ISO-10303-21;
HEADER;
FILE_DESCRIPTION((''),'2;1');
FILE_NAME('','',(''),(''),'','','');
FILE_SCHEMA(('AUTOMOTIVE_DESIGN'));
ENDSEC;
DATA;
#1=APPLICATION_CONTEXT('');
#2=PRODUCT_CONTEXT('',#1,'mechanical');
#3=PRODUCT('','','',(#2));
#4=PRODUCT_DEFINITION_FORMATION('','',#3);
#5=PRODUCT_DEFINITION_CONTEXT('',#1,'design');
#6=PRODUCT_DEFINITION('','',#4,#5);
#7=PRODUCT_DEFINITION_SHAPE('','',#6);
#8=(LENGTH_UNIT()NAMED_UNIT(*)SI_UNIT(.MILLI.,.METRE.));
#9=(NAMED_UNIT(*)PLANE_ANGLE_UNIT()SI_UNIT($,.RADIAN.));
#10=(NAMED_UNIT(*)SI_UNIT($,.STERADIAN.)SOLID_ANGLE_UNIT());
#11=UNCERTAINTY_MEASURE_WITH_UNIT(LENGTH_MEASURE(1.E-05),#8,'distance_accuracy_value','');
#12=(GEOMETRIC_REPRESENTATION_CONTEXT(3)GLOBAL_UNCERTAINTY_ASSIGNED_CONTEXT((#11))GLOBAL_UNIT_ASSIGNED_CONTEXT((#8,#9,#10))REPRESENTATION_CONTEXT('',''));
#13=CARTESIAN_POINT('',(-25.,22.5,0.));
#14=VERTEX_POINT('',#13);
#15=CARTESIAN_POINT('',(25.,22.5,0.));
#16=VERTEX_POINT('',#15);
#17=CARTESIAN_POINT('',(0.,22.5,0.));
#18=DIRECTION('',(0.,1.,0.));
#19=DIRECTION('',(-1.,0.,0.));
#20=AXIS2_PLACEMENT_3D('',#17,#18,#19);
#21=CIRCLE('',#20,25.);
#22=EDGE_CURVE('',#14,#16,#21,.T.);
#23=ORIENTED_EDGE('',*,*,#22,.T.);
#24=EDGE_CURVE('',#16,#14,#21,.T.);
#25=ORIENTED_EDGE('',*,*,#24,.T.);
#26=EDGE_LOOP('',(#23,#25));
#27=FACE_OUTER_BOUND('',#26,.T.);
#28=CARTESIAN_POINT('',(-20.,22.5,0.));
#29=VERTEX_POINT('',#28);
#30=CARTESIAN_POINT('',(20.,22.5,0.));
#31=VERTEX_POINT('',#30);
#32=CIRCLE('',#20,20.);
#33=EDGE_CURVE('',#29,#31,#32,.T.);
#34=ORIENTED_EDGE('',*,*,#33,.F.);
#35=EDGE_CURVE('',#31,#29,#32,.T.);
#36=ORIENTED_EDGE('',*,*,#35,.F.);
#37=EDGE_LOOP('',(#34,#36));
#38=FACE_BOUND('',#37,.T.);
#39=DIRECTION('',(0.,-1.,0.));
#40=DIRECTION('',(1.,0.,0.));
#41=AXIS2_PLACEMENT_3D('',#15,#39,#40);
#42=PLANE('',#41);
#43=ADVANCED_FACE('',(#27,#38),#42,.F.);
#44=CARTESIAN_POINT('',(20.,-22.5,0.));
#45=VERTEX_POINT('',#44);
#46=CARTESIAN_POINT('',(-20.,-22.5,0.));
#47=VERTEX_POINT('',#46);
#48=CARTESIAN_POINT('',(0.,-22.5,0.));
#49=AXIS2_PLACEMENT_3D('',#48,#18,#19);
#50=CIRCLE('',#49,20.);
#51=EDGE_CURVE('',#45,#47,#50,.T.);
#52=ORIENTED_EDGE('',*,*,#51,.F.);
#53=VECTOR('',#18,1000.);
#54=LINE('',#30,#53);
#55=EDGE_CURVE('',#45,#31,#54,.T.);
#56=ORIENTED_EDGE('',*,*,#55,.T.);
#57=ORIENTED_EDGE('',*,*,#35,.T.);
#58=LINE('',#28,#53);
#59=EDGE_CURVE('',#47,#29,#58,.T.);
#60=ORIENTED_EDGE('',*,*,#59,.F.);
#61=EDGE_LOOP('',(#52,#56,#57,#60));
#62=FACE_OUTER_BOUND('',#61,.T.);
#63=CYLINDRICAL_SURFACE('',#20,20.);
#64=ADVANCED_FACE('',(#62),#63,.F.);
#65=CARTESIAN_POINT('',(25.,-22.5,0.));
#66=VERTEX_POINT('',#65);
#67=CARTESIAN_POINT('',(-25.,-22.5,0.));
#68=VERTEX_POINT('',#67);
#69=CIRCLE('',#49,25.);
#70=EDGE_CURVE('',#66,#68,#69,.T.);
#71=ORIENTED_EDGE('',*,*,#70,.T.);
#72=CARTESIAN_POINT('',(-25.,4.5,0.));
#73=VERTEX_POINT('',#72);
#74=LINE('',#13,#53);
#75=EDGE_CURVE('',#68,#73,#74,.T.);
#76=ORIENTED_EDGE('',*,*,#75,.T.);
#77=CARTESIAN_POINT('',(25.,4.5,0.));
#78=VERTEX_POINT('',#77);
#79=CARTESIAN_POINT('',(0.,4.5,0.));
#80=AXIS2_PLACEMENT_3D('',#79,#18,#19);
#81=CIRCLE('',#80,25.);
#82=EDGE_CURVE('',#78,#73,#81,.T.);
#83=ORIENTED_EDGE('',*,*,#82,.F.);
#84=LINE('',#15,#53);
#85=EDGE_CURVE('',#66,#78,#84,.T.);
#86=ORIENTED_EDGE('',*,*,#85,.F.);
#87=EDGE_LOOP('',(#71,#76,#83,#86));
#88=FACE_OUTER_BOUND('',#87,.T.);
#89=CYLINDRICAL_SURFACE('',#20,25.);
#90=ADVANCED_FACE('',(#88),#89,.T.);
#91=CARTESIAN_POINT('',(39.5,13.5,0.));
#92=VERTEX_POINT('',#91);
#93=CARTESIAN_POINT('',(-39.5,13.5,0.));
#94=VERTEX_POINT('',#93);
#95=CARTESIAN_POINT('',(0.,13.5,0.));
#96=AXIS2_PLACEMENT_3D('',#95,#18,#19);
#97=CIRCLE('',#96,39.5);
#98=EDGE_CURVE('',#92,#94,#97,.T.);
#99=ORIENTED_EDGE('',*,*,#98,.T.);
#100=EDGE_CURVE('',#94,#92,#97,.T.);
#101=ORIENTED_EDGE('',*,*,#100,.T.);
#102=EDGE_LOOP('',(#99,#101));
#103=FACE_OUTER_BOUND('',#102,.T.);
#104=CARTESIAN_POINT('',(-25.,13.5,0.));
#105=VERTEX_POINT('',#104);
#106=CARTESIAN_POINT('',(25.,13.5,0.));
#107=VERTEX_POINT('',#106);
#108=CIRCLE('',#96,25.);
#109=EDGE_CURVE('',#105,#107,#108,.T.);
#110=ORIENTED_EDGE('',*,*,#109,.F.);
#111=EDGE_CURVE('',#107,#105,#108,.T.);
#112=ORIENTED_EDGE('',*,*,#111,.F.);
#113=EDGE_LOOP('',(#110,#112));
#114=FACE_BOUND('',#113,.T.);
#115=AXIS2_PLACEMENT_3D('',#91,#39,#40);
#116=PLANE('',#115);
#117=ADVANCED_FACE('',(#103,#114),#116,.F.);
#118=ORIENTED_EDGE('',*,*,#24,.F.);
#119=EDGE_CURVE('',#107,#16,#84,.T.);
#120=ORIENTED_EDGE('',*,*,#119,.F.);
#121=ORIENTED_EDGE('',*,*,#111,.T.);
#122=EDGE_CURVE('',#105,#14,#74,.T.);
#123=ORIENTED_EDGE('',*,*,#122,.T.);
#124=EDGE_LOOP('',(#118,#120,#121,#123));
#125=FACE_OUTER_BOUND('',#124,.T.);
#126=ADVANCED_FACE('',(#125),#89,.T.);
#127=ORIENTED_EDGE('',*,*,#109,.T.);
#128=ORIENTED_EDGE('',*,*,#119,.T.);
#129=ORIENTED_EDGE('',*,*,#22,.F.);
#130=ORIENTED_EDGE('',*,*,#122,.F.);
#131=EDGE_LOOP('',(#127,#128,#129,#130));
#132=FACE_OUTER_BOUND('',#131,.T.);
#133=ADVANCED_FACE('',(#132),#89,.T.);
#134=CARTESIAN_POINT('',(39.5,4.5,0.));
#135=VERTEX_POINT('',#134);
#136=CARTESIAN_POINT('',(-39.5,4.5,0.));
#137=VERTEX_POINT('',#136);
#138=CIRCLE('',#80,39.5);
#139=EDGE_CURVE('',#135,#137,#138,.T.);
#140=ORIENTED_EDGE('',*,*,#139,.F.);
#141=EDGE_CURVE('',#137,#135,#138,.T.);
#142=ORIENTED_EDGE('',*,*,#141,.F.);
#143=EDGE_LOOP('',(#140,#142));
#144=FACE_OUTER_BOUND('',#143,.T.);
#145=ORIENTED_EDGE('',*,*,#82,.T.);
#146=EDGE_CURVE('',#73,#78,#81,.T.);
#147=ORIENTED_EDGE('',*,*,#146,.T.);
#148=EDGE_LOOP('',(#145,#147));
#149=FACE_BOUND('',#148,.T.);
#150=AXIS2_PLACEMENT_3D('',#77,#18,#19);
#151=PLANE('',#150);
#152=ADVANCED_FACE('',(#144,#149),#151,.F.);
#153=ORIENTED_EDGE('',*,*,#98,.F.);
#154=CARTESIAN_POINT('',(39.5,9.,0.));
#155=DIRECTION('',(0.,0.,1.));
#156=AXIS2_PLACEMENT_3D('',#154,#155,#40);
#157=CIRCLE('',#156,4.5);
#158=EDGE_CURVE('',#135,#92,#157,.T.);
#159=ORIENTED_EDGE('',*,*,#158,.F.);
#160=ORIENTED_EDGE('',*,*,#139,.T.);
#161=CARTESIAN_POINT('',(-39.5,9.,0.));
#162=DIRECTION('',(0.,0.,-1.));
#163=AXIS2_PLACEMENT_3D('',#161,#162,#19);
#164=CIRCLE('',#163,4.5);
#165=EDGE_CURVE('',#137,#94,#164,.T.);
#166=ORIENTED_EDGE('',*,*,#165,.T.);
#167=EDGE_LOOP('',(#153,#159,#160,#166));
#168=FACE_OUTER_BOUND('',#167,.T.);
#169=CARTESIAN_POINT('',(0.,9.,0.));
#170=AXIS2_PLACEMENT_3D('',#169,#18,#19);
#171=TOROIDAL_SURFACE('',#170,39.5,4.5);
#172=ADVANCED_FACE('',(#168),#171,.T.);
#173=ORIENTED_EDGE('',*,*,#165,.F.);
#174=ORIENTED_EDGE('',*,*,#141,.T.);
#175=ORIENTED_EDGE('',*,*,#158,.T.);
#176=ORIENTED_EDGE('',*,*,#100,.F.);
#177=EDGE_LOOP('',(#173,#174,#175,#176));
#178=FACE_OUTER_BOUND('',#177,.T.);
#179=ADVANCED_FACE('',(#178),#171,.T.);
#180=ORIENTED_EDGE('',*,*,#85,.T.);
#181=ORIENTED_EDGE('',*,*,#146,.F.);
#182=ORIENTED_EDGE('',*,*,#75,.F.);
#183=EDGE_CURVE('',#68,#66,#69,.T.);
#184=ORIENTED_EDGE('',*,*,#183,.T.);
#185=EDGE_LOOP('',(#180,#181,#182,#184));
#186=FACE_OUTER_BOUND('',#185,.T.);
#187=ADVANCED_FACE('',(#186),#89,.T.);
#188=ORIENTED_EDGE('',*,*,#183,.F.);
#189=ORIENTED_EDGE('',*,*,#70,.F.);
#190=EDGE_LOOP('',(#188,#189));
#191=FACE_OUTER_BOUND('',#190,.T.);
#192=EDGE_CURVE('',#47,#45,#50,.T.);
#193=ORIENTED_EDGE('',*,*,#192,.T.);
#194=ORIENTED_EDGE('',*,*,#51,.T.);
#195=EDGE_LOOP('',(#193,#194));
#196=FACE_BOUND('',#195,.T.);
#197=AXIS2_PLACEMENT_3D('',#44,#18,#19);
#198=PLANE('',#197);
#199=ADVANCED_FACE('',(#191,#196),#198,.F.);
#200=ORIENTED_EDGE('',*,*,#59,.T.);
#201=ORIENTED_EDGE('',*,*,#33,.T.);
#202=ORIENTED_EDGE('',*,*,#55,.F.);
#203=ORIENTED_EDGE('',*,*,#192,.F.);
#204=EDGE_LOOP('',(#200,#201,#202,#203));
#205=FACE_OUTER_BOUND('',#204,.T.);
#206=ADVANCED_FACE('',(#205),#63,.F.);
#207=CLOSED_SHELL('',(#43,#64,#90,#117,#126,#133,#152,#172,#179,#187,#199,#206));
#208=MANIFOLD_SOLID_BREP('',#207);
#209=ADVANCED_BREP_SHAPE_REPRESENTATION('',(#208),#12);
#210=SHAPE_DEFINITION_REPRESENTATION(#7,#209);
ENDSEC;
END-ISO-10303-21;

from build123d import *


with BuildPart() as part:
    # Sketch1 → Revolve1 (revolve)
    with BuildSketch(Plane.XY, mode=Mode.PRIVATE) as revolve1_sk:
        with BuildLine():
            Line((20, 22.5), (20, -22.5))
            Line((20, -22.5), (25, -22.5))
            Line((25, -22.5), (25, 4.5))
            Line((25, 4.5), (39.5, 4.5))
            ThreePointArc((39.5, 4.5), (44, 9), (39.5, 13.5))
            Line((39.5, 13.5), (25, 13.5))
            Line((25, 13.5), (25, 22.5))
            Line((25, 22.5), (20, 22.5))
        make_face()
    revolve(revolve1_sk.sketch.rotate(Axis((0, 22.5, 0), (0, -1, 0)), 180), axis=Axis((0, 22.5, 0), (0, -1, 0)))


solid = part.part
